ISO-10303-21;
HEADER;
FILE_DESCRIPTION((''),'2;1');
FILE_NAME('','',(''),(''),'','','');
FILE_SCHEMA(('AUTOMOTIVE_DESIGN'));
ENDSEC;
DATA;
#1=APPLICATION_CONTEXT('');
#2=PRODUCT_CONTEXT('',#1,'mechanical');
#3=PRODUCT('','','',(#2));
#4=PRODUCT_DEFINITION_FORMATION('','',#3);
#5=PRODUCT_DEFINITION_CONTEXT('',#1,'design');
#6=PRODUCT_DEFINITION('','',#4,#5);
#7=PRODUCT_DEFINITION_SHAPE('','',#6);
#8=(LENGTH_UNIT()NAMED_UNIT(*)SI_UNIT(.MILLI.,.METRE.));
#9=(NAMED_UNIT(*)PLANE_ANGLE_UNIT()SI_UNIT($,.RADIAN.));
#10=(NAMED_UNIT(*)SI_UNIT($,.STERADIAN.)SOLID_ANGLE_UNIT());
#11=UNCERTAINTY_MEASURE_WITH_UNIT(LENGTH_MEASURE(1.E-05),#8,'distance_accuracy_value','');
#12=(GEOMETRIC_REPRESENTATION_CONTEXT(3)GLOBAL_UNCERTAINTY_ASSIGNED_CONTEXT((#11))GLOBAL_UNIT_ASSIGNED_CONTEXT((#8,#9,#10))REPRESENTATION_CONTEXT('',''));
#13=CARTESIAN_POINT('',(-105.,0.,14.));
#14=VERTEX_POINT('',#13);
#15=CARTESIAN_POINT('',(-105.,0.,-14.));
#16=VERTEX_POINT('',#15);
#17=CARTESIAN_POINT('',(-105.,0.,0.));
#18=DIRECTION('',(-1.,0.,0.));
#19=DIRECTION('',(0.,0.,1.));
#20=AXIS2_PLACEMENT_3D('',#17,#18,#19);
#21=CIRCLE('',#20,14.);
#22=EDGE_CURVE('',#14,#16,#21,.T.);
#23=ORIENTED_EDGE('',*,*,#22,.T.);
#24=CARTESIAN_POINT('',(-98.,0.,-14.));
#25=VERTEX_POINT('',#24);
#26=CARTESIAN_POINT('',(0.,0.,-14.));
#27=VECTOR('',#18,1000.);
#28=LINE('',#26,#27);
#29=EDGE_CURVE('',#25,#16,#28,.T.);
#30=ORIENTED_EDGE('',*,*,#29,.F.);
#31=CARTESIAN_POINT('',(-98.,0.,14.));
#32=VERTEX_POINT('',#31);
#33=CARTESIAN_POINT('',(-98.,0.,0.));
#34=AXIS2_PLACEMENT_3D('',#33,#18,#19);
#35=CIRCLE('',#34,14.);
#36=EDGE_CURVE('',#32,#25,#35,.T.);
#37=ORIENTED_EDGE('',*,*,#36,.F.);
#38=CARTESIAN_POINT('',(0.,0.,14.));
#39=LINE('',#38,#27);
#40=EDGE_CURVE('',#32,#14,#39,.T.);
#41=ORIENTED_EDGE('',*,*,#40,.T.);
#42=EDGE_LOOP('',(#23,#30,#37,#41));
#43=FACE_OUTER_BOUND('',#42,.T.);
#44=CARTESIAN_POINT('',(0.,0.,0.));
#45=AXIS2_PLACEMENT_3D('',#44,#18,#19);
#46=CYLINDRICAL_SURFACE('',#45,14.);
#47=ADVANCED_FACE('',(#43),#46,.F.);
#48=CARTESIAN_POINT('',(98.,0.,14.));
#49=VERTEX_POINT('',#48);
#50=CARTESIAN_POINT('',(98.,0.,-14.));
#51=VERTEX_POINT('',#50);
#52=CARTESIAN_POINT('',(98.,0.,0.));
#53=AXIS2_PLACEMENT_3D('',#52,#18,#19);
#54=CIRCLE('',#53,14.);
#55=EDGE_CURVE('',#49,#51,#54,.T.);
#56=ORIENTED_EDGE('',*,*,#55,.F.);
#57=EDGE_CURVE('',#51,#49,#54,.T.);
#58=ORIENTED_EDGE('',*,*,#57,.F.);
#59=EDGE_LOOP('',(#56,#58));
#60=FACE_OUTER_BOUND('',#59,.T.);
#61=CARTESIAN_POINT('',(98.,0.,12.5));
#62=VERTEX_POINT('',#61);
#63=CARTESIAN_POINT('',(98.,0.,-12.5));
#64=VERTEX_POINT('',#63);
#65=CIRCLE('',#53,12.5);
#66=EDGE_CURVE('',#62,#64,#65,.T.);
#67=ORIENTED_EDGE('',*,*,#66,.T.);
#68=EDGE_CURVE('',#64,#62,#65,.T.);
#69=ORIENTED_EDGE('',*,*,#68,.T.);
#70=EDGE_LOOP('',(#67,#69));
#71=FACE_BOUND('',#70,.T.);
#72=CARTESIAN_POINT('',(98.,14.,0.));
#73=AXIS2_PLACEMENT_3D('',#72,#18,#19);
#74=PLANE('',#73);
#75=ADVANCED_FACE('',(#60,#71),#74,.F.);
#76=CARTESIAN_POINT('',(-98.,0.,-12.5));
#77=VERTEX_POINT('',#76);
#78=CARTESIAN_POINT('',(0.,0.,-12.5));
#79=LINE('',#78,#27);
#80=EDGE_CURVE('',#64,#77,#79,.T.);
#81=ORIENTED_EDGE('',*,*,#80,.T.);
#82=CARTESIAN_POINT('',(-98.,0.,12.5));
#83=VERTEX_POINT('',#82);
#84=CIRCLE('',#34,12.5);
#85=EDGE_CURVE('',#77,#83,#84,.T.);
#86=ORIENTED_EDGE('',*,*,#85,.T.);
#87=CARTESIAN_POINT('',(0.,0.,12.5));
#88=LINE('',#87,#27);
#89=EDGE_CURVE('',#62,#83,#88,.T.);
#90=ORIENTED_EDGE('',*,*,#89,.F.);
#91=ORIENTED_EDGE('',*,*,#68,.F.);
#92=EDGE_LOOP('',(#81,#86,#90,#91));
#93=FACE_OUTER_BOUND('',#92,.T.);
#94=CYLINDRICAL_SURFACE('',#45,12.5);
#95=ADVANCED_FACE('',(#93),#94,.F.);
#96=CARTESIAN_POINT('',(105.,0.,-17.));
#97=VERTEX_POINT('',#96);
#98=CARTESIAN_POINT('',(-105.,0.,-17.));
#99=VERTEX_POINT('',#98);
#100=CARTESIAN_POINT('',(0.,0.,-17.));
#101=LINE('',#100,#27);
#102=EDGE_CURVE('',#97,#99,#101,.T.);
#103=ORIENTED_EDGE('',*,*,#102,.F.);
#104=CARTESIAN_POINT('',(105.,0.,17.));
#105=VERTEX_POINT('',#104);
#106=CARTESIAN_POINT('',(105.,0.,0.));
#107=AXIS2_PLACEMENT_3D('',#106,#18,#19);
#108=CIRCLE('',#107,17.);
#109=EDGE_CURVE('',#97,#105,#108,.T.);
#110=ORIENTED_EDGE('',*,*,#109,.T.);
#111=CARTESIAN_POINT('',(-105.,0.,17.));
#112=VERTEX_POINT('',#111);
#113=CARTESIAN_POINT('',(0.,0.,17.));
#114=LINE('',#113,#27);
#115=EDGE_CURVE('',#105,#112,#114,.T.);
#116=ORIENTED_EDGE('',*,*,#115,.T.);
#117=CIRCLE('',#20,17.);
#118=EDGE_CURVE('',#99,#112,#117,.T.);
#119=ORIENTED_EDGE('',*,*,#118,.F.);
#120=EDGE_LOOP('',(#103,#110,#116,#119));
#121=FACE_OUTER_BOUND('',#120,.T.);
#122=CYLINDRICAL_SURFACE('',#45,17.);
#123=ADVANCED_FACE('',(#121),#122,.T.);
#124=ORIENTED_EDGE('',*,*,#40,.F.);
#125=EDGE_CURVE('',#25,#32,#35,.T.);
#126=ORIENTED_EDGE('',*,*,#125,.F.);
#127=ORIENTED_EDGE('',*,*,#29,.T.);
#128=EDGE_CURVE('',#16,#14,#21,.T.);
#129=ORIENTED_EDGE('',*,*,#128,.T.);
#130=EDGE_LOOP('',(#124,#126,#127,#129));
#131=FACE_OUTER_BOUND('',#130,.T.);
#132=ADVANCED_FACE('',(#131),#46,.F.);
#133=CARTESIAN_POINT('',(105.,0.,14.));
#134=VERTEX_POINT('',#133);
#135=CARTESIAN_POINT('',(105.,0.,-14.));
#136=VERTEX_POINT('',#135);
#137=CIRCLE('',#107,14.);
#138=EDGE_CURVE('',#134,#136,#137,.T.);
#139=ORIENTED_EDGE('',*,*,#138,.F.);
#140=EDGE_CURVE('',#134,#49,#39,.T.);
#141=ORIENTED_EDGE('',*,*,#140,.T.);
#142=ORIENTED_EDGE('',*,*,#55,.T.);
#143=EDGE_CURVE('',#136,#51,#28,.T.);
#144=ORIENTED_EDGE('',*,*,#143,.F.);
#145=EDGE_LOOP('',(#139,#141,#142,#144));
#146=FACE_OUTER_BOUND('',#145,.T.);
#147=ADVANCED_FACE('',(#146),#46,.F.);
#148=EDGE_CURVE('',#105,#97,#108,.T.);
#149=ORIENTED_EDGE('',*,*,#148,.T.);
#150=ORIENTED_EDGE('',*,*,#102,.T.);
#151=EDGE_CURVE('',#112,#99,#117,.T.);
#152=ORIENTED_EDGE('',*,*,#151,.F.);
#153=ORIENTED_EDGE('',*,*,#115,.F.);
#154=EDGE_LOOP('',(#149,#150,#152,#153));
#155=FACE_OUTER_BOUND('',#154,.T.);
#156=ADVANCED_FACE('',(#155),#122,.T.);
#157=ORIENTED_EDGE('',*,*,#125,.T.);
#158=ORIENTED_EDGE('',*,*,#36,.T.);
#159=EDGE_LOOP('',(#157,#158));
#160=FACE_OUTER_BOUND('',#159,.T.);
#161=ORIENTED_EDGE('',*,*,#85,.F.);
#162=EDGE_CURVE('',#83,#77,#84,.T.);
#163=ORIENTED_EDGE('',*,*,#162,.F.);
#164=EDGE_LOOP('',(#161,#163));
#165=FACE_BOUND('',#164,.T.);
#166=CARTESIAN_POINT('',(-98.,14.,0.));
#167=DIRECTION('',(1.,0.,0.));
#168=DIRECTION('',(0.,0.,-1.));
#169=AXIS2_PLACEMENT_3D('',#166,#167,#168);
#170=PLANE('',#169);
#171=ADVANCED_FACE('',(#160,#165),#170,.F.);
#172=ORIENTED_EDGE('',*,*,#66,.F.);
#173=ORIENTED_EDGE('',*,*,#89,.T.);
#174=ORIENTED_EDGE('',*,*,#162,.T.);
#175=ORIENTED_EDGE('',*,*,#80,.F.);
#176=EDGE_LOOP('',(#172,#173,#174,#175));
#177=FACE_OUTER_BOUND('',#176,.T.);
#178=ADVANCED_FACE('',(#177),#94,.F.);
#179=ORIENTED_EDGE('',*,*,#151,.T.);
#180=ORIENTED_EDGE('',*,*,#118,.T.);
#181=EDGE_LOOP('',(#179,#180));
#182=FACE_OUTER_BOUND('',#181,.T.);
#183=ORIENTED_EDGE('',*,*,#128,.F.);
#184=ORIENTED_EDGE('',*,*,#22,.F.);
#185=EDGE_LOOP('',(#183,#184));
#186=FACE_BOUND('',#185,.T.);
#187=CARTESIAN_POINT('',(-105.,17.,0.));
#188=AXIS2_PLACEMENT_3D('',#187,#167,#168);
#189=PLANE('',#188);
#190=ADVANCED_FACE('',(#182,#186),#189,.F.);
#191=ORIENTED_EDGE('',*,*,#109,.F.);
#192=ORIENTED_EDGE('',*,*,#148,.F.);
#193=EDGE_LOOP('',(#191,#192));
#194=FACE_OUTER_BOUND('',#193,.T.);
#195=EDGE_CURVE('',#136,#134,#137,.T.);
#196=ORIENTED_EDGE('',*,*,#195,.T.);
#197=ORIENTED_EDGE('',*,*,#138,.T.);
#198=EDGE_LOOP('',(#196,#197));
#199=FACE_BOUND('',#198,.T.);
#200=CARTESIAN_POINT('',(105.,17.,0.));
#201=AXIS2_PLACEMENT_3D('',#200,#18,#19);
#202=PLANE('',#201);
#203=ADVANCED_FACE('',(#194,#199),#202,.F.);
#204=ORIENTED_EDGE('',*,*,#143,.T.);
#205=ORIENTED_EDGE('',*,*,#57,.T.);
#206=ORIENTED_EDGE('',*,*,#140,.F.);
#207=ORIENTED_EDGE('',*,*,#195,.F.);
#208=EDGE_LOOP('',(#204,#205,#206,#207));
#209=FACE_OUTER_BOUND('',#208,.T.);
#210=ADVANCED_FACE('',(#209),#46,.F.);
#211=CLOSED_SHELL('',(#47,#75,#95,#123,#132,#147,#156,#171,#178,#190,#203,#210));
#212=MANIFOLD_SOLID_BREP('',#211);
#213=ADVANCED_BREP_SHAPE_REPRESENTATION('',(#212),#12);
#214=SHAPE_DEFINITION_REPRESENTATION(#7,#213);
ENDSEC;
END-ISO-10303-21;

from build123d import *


with BuildPart() as part:
    # 草图1 → 旋转1 (revolve)
    with BuildSketch(Plane.XY, mode=Mode.PRIVATE) as revolve_1_sk:
        Polygon((105, 17), (-105, 17), (-105, 14), (-98, 14), (-98, 12.5), (98, 12.5), (98, 14), (105, 14), align=None)
    revolve(revolve_1_sk.sketch.rotate(Axis((0, 0, 0), (1, 0, 0)), 90), axis=Axis((0, 0, 0), (1, 0, 0)))


solid = part.part
